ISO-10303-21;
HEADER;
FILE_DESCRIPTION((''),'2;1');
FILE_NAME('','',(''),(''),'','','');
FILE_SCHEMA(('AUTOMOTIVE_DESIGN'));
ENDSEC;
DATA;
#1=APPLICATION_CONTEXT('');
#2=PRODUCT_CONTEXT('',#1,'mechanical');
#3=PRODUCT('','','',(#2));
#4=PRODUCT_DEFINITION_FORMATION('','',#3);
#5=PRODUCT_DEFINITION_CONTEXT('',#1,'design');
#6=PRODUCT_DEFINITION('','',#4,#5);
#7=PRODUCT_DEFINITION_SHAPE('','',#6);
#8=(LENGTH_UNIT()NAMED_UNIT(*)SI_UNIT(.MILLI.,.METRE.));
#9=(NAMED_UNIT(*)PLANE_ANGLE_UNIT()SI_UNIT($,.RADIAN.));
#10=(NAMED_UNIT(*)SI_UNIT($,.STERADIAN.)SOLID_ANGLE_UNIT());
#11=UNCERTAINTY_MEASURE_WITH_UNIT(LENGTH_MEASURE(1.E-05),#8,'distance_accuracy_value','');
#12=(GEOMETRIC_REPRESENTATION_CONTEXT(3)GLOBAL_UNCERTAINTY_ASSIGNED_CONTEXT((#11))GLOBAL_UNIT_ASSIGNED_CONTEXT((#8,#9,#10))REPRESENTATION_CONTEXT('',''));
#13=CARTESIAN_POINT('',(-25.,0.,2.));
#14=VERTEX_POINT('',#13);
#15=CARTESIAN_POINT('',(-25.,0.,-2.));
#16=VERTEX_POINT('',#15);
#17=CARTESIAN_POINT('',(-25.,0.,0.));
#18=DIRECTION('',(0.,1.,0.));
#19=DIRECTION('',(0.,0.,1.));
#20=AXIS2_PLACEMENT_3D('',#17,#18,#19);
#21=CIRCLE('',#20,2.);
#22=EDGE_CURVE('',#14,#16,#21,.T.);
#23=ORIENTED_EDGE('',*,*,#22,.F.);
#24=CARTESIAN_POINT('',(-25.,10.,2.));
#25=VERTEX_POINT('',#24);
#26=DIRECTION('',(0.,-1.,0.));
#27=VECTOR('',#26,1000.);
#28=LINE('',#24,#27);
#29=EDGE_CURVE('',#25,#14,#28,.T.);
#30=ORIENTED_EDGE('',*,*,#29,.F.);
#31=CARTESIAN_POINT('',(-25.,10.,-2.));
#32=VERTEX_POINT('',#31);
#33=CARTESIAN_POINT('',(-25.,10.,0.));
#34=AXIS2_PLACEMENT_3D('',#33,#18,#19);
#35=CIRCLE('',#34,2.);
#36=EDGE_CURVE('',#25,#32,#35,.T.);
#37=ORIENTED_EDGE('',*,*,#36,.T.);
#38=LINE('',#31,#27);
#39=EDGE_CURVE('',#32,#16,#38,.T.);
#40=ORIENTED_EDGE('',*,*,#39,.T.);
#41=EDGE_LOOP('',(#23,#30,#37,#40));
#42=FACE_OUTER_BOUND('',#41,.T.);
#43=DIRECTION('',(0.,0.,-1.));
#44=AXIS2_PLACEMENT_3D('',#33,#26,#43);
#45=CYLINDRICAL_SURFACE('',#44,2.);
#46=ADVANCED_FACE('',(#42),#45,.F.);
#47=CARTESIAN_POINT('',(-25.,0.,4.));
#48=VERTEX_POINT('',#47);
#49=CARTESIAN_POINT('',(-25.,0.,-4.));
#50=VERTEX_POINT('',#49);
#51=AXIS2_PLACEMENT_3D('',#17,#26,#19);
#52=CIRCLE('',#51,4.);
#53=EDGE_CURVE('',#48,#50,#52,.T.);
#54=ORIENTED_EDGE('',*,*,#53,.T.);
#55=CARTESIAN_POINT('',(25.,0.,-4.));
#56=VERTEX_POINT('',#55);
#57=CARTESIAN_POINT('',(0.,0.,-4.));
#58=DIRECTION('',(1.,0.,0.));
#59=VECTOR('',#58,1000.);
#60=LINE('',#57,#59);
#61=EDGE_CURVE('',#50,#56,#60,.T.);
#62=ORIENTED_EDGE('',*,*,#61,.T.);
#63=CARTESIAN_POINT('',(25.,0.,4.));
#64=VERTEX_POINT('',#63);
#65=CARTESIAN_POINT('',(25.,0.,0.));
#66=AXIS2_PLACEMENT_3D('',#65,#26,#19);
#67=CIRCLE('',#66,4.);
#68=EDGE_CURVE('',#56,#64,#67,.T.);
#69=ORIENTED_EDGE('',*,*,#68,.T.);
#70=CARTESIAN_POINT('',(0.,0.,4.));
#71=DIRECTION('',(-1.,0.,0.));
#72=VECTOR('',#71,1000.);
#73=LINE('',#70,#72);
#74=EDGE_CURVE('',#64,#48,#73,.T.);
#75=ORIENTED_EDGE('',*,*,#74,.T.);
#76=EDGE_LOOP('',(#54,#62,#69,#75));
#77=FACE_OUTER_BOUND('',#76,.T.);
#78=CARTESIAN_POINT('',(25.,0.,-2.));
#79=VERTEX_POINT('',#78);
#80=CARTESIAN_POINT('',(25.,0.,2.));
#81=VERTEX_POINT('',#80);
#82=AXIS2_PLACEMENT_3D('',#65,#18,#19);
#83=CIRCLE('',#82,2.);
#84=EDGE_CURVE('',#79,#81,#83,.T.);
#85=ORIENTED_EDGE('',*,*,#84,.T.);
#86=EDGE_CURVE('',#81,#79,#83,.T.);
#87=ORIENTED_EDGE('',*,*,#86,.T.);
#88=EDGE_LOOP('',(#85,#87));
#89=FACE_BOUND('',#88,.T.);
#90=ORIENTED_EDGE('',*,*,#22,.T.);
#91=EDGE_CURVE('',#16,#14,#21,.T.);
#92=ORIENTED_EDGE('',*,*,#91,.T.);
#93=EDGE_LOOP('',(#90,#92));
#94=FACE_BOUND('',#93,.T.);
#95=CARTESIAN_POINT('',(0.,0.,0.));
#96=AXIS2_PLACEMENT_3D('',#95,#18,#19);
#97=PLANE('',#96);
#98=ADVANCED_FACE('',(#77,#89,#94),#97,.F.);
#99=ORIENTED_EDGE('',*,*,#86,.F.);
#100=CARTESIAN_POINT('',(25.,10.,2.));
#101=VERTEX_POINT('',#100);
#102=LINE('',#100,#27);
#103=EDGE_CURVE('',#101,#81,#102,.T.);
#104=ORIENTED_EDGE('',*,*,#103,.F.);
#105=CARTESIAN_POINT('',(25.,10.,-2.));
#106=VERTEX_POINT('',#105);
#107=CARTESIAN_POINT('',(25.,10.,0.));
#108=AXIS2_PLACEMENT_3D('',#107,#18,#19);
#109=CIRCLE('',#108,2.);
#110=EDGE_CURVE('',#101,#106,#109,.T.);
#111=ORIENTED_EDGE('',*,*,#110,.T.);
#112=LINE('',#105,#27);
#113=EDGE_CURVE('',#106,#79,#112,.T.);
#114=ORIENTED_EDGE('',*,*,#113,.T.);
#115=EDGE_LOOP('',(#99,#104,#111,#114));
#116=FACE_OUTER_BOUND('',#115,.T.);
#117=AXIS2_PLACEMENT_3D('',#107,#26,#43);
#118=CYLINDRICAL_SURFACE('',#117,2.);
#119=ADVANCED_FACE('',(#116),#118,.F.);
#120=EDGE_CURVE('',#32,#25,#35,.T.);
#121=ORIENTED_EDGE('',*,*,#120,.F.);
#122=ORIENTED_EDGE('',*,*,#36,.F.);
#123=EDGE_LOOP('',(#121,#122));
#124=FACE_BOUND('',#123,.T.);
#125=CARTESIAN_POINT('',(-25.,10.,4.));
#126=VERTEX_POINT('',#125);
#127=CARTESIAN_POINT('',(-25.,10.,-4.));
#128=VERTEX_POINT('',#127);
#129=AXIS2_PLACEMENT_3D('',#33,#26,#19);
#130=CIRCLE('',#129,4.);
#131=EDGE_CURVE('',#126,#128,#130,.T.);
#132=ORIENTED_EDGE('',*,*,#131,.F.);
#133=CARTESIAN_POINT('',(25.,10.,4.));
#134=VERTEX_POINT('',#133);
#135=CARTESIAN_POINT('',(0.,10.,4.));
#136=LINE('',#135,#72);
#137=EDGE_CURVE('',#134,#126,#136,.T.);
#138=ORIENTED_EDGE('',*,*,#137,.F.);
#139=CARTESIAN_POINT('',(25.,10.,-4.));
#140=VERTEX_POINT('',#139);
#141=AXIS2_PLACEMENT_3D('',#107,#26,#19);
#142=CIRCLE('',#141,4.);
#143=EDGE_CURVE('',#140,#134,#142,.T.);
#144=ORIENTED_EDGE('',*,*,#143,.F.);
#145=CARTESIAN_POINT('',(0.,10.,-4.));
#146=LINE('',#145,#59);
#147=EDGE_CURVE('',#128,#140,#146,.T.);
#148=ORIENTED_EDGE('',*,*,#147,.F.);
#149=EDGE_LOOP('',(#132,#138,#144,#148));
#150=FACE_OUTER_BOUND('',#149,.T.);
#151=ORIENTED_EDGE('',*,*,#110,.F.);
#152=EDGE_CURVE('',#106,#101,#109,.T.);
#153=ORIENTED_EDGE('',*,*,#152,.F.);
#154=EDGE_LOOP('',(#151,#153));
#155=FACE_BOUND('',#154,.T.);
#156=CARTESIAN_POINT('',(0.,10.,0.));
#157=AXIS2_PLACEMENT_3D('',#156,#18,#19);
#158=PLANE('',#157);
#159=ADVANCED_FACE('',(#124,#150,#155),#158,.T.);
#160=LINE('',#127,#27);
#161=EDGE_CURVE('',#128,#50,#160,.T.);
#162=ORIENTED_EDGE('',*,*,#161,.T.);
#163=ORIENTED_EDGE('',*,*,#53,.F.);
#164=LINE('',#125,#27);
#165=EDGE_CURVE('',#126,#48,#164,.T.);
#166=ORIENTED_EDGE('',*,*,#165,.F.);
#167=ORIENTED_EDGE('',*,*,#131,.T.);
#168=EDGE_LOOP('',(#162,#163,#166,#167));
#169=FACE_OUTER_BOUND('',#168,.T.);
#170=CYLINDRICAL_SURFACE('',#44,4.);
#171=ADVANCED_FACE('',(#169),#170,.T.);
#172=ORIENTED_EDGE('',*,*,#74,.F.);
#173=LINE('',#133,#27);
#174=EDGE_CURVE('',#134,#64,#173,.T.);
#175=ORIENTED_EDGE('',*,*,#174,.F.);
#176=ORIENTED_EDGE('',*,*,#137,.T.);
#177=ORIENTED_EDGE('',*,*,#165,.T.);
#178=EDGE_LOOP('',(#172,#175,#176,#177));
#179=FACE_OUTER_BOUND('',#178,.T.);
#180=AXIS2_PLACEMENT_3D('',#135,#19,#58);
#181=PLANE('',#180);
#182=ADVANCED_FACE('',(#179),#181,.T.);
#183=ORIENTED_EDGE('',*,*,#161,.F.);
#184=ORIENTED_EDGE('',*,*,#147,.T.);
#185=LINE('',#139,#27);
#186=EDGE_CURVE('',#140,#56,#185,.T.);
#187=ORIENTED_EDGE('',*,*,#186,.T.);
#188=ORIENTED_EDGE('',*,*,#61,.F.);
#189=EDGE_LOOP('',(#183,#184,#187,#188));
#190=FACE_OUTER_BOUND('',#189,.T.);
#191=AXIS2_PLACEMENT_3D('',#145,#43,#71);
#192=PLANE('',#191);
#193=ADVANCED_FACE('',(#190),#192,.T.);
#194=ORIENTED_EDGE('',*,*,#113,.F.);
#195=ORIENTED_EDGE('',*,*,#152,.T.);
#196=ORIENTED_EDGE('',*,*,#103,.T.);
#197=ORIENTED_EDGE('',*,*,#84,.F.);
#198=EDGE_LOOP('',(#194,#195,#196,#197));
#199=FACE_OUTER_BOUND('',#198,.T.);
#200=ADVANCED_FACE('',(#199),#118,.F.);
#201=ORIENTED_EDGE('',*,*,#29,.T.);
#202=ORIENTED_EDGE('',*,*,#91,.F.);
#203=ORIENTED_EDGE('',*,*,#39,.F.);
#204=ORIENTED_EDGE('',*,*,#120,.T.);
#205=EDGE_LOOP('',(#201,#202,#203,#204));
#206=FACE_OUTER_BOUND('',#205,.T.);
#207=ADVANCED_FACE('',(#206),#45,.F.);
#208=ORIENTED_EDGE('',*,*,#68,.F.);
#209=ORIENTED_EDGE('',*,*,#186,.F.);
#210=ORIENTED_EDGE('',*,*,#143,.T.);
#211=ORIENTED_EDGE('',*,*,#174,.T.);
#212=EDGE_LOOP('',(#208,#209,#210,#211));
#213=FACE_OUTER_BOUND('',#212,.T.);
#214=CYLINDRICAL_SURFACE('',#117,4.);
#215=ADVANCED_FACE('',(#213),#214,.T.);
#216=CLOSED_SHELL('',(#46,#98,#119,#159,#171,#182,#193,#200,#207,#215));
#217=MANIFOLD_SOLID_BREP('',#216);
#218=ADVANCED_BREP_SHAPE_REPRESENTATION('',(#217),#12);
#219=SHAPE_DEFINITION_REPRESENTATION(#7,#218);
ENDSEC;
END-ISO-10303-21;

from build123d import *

# Parameters (mm, degrees)
SKETCH1_R           = 2
BOSS_EXTRUDE1_DEPTH = 10


with BuildPart() as part:
    # Sketch1 → Boss-Extrude1 (new body)
    with BuildSketch(Plane(origin=(0, 0, 0), x_dir=(1, 0, 0), z_dir=(0, 1, 0))):
        with BuildLine():
            Line((-25, 4), (25, 4))
            ThreePointArc((25, 4), (29, 0), (25, -4))
            Line((25, -4), (-25, -4))
            ThreePointArc((-25, -4), (-29, 0), (-25, 4))
        make_face()
        with Locations(Location((-25, 0, 0), (0, 0, 270))):
            Circle(SKETCH1_R, mode=Mode.SUBTRACT)
        with Locations(Location((25, 0, 0), (0, 0, 270))):
            Circle(SKETCH1_R, mode=Mode.SUBTRACT)
    extrude(amount=BOSS_EXTRUDE1_DEPTH)


solid = part.part
